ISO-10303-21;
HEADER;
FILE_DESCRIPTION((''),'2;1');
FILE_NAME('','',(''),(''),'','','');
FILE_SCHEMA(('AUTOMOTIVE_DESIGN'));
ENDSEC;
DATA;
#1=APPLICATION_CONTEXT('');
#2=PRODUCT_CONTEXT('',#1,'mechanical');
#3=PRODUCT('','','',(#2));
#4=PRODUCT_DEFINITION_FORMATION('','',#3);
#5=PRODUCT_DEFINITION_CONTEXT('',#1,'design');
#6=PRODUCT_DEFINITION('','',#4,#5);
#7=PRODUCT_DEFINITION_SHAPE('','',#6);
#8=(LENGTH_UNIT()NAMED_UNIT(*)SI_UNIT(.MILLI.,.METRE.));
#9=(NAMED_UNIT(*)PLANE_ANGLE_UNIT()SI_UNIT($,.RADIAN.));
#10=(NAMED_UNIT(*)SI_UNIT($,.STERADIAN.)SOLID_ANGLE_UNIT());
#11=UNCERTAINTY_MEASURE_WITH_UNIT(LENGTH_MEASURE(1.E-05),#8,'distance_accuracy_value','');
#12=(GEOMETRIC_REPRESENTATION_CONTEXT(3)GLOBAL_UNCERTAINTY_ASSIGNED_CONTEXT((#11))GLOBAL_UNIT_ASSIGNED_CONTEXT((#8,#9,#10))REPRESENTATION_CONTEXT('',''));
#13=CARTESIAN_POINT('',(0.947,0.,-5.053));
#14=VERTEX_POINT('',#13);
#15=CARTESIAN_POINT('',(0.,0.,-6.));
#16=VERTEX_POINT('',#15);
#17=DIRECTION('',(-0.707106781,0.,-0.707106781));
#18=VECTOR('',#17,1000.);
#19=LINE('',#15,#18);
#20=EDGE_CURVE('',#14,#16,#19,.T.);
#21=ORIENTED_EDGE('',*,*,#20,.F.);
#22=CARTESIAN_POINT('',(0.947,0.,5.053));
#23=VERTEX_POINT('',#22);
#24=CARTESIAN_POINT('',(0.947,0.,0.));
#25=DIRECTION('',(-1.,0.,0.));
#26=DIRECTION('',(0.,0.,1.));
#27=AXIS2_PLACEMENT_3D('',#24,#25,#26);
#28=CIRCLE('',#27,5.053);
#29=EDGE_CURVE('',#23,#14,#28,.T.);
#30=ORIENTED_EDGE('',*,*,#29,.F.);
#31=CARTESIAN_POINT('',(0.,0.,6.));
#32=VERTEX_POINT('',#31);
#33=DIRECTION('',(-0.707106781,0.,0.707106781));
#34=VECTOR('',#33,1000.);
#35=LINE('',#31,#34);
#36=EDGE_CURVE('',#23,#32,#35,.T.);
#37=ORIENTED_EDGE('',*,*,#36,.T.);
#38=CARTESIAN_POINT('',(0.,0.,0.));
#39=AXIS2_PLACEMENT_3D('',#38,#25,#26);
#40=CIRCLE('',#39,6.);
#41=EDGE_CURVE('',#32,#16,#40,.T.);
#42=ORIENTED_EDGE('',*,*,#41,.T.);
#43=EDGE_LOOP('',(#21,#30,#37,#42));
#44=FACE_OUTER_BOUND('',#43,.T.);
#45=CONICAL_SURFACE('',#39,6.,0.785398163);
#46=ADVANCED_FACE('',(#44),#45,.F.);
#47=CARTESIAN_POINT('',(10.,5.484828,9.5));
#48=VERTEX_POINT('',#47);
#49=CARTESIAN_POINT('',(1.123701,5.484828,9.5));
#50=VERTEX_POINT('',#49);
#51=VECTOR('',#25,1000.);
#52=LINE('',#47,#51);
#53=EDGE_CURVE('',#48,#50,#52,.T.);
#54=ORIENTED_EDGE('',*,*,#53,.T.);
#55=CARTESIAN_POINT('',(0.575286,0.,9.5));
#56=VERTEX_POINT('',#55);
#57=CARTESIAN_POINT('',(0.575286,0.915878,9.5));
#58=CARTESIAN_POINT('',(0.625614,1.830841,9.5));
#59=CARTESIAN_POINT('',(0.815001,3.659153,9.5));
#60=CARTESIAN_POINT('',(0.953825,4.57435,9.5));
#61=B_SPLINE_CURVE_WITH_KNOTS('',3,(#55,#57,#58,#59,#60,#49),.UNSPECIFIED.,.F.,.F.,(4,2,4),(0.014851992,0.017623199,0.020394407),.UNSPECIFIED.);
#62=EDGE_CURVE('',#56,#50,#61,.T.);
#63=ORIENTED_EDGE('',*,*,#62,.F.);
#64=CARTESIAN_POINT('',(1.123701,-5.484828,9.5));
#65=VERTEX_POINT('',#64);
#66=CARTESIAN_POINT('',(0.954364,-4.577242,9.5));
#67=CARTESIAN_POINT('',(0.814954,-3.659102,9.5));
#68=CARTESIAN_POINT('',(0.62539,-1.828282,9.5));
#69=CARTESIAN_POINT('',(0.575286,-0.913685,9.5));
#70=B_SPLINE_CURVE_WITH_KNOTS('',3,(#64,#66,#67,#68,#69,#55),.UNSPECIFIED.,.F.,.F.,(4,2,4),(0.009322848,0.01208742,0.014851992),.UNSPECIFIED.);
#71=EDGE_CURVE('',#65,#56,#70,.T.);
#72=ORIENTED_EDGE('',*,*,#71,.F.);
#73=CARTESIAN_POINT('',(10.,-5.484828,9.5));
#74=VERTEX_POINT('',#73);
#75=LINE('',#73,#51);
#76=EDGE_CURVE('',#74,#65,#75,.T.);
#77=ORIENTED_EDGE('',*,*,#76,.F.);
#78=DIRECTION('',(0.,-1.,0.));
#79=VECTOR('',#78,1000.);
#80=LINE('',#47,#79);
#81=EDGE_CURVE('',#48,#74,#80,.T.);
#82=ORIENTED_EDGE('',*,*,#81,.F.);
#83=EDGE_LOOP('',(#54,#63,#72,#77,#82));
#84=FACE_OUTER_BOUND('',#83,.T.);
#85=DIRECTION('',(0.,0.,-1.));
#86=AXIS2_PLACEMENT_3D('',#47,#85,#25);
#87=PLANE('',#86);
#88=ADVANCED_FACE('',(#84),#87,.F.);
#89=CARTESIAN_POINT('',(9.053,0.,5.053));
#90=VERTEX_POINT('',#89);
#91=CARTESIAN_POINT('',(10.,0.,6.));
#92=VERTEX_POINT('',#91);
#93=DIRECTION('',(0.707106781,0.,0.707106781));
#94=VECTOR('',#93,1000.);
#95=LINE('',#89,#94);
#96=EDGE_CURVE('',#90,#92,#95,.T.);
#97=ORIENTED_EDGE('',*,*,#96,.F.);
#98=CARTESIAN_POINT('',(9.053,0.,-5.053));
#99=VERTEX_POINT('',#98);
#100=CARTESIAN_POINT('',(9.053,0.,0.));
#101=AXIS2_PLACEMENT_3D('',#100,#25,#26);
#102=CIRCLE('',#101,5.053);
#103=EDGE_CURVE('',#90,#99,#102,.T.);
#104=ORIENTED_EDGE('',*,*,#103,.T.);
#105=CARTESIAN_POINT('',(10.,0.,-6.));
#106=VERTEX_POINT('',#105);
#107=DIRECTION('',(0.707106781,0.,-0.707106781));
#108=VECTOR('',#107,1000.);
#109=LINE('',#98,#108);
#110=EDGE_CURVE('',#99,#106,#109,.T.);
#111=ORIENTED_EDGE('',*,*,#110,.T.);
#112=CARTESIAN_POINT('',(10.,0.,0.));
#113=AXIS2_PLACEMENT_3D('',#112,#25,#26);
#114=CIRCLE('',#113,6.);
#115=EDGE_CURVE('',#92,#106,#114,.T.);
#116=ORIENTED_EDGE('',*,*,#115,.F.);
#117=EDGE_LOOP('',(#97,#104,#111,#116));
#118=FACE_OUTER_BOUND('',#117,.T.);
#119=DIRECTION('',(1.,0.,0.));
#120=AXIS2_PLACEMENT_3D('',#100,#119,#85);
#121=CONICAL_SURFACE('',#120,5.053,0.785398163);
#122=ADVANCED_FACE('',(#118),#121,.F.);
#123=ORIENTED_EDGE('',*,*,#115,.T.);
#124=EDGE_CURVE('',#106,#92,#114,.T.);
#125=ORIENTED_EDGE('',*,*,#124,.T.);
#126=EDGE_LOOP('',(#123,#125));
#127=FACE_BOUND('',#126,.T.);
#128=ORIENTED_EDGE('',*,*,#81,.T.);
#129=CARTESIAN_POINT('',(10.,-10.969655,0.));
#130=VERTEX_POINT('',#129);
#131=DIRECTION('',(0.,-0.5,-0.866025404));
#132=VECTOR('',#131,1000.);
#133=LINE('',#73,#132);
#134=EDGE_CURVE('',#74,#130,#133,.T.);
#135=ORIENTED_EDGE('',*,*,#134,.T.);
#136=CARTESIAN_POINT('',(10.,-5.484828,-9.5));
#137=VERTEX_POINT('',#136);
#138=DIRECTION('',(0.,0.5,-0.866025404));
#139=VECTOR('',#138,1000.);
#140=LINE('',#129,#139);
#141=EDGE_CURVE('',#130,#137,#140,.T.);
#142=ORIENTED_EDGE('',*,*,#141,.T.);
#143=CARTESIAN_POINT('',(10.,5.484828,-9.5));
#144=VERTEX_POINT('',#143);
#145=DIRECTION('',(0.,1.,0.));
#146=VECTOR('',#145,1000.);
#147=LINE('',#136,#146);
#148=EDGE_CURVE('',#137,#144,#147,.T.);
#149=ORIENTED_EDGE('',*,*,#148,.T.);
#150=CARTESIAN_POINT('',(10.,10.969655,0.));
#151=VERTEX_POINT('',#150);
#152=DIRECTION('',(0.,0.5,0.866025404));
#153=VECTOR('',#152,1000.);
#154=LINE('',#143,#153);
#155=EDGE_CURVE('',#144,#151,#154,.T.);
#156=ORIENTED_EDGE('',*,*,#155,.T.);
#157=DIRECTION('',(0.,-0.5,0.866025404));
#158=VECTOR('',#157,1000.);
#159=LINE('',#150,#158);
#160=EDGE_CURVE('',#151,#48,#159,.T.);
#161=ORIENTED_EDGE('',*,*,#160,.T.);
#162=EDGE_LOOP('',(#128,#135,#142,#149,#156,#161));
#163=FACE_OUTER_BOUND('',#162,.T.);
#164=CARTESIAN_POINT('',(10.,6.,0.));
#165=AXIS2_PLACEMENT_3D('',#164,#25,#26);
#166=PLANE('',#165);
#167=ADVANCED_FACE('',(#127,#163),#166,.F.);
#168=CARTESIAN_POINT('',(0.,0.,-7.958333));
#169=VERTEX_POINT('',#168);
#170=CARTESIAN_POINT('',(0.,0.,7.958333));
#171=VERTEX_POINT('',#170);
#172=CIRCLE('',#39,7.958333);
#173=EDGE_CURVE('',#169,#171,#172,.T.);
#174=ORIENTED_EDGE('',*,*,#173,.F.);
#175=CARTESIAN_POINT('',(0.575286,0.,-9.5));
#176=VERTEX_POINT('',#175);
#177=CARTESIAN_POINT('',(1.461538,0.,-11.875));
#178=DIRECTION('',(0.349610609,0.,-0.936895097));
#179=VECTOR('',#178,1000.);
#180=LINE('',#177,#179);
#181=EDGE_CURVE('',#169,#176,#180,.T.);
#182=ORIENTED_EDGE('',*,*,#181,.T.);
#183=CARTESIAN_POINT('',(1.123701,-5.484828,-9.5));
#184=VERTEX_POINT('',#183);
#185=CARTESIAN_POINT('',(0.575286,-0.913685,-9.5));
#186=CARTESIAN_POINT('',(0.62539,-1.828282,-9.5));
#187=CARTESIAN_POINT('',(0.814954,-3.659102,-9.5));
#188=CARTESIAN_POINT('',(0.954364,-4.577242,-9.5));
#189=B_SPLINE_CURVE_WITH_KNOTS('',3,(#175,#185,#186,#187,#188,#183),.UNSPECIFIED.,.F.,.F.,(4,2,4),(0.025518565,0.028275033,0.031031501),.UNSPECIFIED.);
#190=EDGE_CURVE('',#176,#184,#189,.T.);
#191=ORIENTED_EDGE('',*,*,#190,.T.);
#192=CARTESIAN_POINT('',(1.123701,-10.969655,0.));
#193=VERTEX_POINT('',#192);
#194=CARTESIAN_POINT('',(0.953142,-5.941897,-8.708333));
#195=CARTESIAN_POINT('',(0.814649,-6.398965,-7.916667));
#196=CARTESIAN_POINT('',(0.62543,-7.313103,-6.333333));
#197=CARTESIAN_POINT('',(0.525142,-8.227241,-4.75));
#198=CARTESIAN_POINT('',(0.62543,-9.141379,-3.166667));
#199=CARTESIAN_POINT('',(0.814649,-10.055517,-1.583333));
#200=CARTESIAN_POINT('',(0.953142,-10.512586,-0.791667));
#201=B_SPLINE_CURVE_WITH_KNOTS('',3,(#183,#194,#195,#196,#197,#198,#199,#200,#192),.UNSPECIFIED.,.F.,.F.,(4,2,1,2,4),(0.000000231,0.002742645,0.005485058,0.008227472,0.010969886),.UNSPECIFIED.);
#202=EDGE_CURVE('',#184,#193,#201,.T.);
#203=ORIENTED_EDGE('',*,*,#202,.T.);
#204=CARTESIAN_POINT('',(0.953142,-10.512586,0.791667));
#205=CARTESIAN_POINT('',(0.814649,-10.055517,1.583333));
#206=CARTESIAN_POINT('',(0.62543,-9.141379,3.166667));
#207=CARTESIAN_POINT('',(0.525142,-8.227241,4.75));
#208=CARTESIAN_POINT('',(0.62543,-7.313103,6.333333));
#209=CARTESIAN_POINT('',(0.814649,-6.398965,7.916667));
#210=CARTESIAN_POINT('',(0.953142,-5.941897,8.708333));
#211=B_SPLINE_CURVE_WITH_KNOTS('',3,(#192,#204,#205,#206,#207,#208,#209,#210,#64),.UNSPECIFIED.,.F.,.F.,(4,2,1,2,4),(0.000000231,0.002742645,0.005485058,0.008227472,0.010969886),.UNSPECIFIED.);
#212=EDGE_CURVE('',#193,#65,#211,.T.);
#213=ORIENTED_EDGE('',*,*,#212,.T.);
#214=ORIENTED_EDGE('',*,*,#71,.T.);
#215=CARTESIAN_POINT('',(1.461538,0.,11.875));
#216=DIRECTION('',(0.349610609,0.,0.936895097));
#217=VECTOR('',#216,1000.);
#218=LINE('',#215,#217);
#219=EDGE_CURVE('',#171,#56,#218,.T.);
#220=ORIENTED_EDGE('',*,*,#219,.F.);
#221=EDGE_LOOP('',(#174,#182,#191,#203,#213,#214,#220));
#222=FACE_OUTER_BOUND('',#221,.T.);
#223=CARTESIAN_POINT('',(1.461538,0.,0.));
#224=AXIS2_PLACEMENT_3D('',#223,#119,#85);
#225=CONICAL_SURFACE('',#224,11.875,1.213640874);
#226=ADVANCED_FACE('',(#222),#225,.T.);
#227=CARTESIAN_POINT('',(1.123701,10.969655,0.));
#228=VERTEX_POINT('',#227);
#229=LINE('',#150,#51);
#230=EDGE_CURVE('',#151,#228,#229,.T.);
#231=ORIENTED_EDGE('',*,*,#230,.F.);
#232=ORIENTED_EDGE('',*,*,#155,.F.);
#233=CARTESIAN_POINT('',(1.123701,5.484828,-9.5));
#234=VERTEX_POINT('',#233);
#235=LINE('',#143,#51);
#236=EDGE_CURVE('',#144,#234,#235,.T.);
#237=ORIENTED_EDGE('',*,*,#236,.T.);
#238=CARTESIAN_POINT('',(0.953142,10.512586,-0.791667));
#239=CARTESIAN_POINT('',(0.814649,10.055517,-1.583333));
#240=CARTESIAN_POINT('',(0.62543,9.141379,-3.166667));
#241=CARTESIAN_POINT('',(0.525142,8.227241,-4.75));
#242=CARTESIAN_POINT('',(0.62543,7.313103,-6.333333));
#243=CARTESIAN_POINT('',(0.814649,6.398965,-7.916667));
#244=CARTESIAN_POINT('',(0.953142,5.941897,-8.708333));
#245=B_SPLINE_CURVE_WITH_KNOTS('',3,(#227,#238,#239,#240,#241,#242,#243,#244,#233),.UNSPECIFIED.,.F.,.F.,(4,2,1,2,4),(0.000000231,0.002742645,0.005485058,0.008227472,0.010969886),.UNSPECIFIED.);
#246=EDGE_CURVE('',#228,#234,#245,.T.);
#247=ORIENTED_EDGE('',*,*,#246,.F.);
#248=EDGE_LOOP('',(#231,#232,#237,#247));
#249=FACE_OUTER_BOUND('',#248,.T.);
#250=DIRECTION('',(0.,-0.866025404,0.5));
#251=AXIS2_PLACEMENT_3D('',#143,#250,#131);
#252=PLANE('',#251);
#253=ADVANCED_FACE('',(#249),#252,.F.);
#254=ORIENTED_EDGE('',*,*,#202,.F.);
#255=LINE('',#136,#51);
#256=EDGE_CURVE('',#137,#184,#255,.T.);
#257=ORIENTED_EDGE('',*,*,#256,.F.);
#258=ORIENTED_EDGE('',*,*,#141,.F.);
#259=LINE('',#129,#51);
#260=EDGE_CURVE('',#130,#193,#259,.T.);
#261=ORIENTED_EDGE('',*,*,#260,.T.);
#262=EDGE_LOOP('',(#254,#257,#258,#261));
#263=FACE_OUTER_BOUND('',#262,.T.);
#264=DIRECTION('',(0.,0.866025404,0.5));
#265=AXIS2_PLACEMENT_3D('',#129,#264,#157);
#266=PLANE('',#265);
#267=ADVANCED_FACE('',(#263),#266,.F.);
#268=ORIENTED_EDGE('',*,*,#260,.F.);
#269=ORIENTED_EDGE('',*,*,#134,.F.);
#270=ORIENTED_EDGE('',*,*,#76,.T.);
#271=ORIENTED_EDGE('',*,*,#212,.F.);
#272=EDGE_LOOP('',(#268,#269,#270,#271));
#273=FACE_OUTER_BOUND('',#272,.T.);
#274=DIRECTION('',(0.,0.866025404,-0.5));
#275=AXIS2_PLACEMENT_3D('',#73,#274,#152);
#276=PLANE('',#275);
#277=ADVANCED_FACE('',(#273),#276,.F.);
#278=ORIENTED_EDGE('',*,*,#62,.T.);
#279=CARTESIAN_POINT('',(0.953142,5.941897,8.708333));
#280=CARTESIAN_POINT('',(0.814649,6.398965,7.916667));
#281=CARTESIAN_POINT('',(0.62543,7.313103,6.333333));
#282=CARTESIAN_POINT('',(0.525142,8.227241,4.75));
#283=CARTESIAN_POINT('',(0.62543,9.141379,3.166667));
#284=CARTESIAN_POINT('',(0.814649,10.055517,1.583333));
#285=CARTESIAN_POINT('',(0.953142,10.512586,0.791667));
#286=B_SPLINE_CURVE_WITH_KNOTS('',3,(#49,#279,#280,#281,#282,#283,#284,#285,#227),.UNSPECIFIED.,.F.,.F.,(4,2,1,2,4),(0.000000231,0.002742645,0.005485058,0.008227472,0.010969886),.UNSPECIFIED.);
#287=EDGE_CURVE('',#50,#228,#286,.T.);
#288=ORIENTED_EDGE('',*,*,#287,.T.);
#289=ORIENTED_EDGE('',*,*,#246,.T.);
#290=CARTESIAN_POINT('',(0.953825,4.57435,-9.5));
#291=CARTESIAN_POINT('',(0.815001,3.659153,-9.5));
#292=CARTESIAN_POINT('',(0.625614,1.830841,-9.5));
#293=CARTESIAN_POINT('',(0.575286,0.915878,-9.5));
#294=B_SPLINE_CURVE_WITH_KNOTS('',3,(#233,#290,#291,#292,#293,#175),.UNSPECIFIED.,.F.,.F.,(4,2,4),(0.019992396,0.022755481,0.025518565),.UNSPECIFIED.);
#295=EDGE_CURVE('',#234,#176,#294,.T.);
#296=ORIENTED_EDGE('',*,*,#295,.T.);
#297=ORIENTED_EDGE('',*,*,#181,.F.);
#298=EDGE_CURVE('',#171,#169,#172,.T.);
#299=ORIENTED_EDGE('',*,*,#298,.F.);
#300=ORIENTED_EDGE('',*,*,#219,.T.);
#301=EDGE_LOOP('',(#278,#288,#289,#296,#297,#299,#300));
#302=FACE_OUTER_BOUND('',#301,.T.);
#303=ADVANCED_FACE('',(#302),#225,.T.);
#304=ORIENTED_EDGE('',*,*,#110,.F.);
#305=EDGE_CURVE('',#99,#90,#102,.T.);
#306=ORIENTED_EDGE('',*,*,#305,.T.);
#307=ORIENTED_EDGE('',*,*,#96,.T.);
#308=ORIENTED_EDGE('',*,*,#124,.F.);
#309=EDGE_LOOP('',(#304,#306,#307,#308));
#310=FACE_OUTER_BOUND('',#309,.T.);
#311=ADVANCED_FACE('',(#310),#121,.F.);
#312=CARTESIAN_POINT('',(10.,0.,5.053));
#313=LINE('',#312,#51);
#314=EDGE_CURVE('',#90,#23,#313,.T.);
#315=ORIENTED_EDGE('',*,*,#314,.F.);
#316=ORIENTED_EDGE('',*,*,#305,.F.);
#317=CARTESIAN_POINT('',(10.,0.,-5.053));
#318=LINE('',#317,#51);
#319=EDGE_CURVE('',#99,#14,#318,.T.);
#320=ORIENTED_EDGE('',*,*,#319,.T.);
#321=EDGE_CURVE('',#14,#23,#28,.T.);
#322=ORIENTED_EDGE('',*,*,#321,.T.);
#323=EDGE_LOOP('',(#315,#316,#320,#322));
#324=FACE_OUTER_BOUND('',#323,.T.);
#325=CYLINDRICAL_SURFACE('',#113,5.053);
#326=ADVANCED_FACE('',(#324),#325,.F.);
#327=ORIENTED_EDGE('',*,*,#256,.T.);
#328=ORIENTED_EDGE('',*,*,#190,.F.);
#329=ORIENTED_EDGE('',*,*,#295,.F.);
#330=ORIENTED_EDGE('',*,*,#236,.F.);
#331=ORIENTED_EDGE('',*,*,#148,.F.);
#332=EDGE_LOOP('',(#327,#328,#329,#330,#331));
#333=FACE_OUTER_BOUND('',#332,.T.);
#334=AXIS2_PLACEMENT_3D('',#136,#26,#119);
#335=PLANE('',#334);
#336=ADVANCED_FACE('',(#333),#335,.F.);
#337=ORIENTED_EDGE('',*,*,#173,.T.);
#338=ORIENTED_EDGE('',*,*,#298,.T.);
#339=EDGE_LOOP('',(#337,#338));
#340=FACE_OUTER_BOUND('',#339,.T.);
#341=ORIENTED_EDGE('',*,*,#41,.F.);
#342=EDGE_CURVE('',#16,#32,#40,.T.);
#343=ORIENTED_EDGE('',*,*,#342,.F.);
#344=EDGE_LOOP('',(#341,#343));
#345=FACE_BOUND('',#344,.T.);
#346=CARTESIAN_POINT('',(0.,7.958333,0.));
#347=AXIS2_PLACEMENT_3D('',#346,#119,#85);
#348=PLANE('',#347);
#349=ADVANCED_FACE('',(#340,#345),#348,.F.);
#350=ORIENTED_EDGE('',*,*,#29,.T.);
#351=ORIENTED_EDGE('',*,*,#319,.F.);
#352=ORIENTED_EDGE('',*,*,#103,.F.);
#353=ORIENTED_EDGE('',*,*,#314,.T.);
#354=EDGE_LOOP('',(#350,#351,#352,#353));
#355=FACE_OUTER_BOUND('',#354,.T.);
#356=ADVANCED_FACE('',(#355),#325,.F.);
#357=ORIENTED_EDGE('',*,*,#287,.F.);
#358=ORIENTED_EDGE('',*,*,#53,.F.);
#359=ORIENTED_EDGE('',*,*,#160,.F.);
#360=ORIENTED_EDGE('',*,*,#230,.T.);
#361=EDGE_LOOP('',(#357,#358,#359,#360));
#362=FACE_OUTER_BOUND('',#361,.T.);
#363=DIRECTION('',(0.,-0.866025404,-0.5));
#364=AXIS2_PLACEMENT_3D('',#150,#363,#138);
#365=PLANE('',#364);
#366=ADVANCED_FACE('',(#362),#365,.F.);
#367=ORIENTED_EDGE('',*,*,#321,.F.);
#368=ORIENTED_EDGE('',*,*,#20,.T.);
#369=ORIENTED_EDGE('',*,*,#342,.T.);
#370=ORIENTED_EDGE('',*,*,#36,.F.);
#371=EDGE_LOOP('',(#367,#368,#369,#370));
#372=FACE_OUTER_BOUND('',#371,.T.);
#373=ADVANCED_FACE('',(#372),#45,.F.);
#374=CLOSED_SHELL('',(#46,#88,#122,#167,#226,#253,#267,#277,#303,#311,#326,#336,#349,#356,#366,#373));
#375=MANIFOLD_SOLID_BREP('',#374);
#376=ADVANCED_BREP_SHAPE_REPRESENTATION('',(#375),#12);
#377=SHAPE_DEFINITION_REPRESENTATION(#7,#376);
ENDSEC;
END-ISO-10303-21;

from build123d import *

# Parameters (mm, degrees)
CUT_EXTRUDE_1_DEPTH = 10


with BuildPart() as part:
    # 草图1 → 旋转1 (revolve)
    with BuildSketch(Plane.XY, mode=Mode.PRIVATE) as revolve_1_sk:
        Polygon((0, 7.958333333), (0, 6), (0.947, 5.053), (9.053, 5.053), (10, 6), (10, 11.875), (1.461538462, 11.875), align=None)
    revolve(revolve_1_sk.sketch.rotate(Axis((10, 0, 0), (-1, 0, 0)), 270), axis=Axis((10, 0, 0), (-1, 0, 0)))

    # 草图2 → 切除-拉伸1 (cut)
    with BuildSketch(Plane(origin=(0, 0, 0), x_dir=(0, 0, -1), z_dir=(1, 0, 0))):
        Polygon((-19, 10.969655115), (-19, -10.969655115), (0, -21.939310229), (19, -10.969655115), (19, 10.969655115), (0, 21.939310229), align=None)
        Polygon((-9.5, 5.484827557), (-9.5, -5.484827557), (0, -10.969655115), (9.5, -5.484827557), (9.5, 5.484827557), (0, 10.969655115), align=None, mode=Mode.SUBTRACT)
    extrude(amount=CUT_EXTRUDE_1_DEPTH, mode=Mode.SUBTRACT)


solid = part.part
